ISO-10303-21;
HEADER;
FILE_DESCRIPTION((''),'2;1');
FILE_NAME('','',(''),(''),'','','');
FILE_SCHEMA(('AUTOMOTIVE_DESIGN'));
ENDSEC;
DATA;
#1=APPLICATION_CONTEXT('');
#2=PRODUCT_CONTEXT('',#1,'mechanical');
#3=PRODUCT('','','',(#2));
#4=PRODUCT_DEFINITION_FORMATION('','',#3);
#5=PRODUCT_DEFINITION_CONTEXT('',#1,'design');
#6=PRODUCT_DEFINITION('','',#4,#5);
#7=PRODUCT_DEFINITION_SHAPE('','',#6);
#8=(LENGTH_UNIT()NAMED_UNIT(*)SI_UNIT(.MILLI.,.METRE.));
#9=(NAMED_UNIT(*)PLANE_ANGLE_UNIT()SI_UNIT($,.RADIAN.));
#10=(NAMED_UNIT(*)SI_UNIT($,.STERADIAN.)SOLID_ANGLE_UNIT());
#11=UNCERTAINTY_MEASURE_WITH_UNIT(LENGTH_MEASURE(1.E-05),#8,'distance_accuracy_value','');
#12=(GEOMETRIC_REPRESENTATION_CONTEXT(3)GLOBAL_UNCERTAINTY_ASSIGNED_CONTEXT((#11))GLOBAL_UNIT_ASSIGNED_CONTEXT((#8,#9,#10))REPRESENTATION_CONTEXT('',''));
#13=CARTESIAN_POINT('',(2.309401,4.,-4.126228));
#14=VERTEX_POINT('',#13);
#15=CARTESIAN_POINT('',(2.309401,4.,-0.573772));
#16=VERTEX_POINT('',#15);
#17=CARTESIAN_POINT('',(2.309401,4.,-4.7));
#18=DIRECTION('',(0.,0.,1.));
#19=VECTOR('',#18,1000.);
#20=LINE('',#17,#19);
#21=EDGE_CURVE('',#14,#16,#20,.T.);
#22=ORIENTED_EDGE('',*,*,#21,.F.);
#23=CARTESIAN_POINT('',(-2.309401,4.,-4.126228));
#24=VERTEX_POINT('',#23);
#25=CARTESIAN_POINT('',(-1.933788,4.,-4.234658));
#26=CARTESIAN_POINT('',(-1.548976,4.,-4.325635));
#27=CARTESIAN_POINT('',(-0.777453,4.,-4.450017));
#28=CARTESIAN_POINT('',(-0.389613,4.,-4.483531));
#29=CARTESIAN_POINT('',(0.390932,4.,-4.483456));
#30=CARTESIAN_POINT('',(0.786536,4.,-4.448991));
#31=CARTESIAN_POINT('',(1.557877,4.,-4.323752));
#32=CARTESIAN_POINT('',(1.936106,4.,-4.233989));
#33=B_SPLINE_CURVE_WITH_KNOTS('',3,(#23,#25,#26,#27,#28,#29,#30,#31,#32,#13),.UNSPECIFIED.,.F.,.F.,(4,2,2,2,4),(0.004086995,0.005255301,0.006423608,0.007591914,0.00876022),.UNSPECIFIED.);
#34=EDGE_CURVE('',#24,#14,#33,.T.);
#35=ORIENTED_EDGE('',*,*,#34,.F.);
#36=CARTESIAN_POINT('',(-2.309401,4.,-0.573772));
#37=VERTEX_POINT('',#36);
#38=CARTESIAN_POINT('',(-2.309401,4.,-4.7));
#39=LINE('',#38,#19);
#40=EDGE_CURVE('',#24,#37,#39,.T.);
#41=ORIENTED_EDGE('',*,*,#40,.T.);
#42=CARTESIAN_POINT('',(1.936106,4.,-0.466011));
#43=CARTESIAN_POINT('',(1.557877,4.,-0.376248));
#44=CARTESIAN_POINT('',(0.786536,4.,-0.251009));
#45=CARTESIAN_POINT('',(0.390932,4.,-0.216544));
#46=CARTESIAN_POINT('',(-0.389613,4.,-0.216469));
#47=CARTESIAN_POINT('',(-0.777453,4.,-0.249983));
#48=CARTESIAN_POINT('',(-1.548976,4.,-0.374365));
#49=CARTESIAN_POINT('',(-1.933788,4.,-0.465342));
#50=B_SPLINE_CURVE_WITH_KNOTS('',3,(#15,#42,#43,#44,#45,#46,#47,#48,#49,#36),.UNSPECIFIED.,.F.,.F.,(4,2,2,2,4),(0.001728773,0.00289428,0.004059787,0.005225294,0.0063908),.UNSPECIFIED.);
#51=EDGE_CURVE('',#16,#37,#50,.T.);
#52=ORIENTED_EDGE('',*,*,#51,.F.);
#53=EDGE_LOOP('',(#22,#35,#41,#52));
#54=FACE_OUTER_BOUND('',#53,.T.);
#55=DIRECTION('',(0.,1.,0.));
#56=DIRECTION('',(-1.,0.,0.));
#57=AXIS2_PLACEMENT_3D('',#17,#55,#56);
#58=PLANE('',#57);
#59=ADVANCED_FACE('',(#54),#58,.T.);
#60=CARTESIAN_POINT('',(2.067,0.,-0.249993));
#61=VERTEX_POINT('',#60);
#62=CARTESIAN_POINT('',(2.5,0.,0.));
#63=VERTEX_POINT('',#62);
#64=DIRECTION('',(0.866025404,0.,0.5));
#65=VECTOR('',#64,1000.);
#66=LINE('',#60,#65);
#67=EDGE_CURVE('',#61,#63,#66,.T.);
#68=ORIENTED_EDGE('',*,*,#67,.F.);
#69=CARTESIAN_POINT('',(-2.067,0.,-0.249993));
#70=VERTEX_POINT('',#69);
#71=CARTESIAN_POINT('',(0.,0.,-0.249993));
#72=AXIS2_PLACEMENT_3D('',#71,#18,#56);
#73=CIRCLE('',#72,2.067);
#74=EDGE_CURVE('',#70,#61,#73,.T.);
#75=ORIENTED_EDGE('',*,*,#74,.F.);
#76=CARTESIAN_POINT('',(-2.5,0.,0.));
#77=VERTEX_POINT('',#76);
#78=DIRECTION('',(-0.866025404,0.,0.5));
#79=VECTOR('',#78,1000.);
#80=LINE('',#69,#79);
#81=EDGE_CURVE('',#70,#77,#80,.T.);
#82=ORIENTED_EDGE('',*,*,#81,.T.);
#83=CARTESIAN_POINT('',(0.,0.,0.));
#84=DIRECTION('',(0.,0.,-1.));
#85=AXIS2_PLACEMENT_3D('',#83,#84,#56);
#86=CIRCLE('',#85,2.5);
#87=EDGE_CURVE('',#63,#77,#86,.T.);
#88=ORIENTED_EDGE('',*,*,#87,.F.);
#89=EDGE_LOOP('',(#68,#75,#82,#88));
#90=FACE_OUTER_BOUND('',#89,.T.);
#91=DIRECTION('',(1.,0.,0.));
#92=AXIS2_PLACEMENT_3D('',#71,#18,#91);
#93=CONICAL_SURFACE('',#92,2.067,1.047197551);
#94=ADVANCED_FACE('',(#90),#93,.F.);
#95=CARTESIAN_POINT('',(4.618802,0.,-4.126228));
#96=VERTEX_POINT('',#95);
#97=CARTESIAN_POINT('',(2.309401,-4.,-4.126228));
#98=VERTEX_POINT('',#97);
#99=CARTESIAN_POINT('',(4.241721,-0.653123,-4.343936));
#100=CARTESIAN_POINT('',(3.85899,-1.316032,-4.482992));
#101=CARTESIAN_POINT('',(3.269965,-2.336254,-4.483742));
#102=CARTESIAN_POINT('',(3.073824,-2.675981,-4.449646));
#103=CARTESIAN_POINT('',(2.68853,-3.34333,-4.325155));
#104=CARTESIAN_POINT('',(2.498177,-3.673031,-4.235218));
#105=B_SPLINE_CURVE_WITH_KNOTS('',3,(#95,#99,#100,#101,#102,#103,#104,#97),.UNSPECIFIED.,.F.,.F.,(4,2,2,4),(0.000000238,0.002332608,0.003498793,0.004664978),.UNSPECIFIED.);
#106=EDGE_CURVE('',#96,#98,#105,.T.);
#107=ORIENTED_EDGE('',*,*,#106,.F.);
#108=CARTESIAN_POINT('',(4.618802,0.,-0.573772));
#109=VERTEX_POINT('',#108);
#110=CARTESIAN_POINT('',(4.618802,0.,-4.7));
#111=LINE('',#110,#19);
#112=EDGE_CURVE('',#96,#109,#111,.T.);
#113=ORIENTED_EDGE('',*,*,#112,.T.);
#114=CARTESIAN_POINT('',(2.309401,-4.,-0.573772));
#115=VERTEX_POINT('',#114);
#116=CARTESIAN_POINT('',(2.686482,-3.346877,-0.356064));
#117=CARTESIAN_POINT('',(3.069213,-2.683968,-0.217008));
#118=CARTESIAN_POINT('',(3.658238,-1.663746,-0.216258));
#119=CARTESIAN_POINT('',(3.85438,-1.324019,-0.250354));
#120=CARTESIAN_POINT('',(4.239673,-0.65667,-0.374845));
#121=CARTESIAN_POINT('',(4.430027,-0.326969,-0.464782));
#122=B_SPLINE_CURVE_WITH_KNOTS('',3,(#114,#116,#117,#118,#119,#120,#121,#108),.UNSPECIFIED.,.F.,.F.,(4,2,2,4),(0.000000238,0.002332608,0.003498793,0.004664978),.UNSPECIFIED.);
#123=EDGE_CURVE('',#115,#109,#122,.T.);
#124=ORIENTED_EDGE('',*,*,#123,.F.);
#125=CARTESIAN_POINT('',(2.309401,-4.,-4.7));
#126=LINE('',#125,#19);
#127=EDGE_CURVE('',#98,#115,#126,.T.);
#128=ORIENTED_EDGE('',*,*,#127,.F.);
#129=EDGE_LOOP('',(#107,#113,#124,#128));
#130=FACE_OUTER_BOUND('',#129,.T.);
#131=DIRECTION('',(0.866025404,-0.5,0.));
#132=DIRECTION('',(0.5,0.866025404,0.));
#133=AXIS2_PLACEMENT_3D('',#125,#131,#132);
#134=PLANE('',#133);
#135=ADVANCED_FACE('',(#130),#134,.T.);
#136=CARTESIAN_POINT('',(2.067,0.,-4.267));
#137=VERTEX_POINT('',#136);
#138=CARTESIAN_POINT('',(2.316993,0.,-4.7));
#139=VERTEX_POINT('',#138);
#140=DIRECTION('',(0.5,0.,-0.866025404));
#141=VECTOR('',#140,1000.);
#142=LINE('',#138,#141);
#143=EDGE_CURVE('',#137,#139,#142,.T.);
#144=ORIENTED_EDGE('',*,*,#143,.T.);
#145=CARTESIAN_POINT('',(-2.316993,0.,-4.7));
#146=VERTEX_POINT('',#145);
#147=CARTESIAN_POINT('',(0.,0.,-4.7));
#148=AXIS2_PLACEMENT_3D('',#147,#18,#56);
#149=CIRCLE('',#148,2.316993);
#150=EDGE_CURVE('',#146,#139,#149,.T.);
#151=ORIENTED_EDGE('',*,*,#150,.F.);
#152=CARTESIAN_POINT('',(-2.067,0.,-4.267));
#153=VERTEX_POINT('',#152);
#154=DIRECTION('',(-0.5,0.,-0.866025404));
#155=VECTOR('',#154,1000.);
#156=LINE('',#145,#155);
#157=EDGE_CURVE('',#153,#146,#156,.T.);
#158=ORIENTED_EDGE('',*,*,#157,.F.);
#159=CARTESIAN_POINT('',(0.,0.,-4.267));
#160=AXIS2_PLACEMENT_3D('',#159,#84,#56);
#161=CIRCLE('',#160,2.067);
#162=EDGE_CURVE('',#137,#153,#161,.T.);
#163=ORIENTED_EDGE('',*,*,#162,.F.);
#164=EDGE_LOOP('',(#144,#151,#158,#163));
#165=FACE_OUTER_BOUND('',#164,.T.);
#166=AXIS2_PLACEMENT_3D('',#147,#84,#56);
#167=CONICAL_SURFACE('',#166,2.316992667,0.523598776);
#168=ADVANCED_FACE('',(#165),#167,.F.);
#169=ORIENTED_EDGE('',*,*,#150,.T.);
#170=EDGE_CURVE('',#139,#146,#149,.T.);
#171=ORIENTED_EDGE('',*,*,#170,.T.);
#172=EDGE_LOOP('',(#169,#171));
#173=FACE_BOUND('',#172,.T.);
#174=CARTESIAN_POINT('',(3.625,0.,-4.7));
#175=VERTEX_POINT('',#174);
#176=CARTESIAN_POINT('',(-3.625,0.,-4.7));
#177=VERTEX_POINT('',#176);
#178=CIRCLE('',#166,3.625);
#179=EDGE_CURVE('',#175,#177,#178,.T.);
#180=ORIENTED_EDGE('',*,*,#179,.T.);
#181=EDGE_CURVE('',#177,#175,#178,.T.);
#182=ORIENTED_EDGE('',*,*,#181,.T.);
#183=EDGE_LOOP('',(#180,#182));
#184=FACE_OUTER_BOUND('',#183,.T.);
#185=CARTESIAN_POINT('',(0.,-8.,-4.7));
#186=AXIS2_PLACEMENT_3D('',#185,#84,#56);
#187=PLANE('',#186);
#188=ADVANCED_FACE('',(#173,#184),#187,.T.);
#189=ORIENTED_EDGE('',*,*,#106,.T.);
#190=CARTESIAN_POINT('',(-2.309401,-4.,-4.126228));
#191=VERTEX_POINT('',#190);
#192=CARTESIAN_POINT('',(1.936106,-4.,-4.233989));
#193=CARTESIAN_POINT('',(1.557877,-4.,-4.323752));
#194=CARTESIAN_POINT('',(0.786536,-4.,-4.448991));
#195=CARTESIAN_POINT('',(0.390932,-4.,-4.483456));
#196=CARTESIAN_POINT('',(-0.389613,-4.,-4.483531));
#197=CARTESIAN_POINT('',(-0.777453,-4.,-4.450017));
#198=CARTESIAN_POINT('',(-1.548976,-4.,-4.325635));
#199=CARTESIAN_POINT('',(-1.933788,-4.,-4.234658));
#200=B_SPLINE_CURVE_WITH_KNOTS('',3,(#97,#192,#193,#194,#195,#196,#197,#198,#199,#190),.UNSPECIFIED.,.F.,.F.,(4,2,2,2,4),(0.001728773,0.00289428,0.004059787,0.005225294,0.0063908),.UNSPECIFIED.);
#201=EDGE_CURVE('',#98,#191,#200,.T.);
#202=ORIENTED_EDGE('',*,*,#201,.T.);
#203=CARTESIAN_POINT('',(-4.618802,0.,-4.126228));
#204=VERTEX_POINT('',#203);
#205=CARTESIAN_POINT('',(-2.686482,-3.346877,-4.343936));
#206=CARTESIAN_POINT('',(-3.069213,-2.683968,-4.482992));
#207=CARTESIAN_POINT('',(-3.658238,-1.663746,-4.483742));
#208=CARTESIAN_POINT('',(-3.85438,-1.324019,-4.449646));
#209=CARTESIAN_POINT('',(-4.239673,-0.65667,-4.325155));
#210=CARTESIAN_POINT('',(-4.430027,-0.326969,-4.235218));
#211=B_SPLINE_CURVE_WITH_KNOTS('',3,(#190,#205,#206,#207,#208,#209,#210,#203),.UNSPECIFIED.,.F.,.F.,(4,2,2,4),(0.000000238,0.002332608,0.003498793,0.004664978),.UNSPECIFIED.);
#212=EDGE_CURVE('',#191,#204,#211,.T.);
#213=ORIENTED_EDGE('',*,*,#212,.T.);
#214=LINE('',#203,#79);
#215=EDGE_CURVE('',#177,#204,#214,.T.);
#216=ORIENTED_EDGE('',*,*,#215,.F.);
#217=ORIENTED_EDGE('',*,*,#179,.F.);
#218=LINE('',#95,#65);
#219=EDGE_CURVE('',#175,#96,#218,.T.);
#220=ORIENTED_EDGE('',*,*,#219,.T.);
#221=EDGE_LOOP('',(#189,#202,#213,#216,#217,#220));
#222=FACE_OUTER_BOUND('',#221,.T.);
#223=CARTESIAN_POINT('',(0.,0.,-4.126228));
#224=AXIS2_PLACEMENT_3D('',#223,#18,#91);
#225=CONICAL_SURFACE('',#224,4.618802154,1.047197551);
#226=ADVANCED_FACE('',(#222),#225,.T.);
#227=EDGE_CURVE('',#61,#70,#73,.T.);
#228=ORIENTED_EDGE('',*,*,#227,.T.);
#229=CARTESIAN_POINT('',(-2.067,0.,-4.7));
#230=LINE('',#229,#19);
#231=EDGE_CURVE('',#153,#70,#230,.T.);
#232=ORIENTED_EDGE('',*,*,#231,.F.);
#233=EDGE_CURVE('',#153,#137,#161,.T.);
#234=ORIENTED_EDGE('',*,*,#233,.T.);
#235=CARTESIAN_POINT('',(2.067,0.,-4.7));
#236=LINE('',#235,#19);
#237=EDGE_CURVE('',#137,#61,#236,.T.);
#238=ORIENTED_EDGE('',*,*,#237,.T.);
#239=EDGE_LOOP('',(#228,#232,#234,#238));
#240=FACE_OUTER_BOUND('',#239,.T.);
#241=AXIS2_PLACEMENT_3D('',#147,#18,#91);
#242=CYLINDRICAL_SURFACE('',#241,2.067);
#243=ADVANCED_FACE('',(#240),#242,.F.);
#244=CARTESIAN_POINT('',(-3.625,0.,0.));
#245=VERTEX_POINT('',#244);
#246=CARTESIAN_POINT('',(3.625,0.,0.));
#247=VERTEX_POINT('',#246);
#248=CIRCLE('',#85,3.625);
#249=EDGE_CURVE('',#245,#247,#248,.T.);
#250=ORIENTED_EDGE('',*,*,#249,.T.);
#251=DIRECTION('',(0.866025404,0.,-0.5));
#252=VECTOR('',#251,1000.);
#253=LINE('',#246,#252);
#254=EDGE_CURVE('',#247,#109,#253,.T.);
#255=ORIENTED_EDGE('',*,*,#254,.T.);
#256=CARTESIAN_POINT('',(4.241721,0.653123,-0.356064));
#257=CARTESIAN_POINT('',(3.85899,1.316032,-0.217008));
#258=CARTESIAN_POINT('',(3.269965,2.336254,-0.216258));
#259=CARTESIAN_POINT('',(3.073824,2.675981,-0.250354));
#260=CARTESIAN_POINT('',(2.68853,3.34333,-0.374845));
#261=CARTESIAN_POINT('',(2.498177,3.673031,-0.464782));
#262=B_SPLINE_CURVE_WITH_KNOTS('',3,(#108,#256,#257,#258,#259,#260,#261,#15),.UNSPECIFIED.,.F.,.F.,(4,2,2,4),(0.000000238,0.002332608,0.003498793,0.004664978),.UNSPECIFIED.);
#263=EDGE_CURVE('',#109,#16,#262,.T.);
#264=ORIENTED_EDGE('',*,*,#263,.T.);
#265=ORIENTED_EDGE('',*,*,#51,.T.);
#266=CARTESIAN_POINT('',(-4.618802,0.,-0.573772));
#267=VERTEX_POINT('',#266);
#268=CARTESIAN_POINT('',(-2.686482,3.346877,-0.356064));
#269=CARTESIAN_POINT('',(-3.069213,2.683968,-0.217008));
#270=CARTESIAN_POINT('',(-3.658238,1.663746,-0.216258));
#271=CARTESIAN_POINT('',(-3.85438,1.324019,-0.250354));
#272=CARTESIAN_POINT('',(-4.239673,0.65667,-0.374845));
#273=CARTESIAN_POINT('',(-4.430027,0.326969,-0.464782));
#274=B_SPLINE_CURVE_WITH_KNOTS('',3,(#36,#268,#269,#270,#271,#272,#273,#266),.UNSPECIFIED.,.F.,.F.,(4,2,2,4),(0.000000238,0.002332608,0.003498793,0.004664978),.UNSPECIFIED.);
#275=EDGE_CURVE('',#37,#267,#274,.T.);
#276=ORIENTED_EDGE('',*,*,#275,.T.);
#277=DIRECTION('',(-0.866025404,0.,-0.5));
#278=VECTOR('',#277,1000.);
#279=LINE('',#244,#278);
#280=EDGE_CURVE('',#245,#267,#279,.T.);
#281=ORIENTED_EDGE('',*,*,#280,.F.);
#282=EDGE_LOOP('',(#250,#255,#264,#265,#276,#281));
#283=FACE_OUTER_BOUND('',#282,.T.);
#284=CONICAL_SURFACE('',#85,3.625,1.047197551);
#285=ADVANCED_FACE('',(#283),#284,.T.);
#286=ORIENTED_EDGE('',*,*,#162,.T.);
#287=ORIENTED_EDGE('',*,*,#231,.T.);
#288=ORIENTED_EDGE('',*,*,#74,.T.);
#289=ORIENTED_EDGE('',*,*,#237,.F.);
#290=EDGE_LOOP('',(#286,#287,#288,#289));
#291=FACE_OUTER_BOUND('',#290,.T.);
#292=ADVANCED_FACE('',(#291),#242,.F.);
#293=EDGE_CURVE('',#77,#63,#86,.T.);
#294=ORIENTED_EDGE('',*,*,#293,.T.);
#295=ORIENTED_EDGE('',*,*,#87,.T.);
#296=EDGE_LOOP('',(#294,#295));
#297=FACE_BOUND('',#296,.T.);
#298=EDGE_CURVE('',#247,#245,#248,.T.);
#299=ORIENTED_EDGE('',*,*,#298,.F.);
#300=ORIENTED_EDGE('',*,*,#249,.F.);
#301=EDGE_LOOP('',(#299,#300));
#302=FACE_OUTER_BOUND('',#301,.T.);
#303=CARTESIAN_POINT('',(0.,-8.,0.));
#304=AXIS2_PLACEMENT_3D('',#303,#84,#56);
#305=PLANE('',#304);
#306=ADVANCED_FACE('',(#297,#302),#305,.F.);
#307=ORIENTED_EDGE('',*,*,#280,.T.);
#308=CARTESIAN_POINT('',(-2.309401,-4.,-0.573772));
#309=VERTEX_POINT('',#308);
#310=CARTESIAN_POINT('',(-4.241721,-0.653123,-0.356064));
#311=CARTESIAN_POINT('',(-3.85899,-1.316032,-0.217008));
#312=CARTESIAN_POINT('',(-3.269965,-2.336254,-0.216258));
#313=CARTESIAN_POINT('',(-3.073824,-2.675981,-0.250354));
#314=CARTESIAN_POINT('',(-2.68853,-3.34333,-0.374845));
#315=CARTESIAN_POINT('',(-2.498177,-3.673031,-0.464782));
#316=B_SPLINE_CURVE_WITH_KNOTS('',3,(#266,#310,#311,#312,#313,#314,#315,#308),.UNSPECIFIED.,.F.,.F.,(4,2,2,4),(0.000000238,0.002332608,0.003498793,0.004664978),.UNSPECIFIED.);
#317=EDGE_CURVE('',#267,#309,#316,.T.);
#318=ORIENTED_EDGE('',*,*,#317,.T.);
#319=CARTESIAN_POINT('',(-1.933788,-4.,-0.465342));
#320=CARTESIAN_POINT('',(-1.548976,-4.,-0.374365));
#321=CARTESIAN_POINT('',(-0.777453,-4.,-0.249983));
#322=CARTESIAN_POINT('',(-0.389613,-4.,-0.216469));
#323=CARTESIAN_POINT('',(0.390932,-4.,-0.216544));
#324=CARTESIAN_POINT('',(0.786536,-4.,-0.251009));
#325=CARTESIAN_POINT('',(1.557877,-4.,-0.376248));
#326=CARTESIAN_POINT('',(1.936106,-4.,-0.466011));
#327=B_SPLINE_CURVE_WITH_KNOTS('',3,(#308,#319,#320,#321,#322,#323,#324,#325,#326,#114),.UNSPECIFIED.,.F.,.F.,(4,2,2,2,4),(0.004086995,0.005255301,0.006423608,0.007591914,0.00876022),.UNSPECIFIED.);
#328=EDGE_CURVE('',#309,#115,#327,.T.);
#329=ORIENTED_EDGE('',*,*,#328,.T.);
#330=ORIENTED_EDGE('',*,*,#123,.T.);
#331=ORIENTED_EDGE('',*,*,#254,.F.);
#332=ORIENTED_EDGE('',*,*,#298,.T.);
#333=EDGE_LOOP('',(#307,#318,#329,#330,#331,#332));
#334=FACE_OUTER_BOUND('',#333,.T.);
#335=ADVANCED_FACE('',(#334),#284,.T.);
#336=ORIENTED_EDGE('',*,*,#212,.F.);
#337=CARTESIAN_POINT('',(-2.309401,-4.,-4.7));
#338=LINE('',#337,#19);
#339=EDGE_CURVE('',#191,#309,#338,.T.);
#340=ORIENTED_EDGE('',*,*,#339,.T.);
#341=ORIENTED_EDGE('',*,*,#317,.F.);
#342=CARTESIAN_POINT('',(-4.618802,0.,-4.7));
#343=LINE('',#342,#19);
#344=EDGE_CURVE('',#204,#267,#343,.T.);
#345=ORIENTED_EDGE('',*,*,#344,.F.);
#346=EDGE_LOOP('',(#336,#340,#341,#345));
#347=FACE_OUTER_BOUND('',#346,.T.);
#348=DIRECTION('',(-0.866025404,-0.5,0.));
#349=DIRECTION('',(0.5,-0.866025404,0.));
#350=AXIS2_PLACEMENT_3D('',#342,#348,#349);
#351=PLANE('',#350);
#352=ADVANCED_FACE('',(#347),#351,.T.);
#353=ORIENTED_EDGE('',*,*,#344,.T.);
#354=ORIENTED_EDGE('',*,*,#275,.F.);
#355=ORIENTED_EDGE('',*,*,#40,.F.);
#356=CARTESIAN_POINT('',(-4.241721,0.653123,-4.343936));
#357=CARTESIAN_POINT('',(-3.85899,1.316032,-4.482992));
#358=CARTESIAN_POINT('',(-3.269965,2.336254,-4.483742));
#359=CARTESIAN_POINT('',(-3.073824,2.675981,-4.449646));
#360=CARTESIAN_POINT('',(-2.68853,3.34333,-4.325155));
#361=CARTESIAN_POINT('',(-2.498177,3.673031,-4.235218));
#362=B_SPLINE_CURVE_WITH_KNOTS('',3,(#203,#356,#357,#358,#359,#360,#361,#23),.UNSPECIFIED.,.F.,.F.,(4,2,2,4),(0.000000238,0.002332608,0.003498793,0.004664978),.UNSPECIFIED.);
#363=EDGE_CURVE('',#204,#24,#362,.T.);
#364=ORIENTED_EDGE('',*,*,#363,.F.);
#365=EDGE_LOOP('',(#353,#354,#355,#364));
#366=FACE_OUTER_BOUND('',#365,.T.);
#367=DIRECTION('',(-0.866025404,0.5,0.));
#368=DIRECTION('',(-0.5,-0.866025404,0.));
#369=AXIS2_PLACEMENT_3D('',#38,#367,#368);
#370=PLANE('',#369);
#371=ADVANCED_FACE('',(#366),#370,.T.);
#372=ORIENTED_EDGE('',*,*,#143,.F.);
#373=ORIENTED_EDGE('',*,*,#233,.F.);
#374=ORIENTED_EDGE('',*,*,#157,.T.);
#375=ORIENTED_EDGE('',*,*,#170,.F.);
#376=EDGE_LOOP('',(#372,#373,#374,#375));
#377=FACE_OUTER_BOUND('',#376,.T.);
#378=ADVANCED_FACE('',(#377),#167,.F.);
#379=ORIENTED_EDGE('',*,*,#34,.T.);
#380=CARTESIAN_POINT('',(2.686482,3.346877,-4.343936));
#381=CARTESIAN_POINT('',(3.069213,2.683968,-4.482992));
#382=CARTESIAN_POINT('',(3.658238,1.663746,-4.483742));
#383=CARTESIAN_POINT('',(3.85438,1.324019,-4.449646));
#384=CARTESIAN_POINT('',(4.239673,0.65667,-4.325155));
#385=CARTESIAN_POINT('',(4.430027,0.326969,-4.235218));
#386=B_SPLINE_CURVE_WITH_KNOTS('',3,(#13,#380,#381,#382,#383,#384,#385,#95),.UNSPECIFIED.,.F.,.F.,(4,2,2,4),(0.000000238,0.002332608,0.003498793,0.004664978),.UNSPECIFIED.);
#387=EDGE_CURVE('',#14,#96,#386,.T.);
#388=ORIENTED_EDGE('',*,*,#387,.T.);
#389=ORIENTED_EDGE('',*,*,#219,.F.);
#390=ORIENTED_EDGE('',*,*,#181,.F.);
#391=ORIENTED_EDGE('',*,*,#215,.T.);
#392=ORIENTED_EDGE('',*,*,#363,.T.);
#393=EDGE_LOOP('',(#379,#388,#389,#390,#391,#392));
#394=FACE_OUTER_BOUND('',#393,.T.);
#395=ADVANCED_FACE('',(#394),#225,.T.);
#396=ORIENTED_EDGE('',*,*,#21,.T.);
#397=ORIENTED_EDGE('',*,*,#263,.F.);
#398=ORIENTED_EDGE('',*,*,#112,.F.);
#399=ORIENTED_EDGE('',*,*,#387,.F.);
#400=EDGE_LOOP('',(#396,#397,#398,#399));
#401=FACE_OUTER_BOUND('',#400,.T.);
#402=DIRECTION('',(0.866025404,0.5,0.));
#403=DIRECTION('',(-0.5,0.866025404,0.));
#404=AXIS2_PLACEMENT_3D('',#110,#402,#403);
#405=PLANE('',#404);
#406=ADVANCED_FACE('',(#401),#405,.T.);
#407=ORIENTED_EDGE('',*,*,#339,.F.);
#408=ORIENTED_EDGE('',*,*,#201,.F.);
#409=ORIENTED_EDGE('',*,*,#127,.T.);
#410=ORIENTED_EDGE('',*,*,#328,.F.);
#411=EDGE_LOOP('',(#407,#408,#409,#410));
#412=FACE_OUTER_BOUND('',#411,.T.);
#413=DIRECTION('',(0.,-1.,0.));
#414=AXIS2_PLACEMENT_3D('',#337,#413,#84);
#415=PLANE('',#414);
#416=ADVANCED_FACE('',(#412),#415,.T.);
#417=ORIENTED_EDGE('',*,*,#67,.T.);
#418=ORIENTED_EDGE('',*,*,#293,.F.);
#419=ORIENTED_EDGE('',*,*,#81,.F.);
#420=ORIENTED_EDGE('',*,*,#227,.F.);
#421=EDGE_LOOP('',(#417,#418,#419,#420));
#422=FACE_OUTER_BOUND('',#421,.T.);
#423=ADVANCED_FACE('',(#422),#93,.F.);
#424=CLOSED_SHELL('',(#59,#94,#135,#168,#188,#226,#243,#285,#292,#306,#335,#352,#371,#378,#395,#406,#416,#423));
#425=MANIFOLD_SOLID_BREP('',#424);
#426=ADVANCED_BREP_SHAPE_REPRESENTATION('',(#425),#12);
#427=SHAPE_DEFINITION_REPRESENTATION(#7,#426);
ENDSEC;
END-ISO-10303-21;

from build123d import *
from OCP.BRepFilletAPI import BRepFilletAPI_MakeChamfer

# Parameters (mm, degrees)
SKETCH1_R        = 2.067
BASENUT_DEPTH    = 4.7
ENDCHAMFER_SIZE  = 0.433
ENDCHAMFER_SIZE2 = 0.249992667


with BuildPart() as part:
    # Sketch1 → BaseNut (new body)
    with BuildSketch(Plane.XY):
        Polygon((4.618802154, 0), (2.309401077, 4), (-2.309401077, 4), (-4.618802154, 0), (-2.309401077, -4), (2.309401077, -4), align=None)
        Circle(SKETCH1_R, mode=Mode.SUBTRACT)
    extrude(amount=-BASENUT_DEPTH)

    # Sketch2 → Double-Chamfer (revolve, cut)
    with BuildSketch(Plane(origin=(0, 0, 0), x_dir=(1, 0, 0), z_dir=(0, 1, 0))):
        Polygon((-4.618802154, 4.7), (-3.625, 4.7), (-4.618802154, 4.126228059), align=None)
        Polygon((-4.618802154, 0.573771941), (-4.618802154, 0), (-3.625, 0), align=None)
    revolve(axis=Axis((0, 0, -3.375940562), (0, 0, 1)), mode=Mode.SUBTRACT)

    # EndChamfer: one chamfer whose edges measure the first distance from different faces: ONE call of the kernel's chamfer builder (chamfer() names one face for all edges)
    endchamfer_edges_1 = [part.edges().sort_by_distance(p)[0] for p in [
        (-2.067, 0, -4.7),
    ]]
    endchamfer_side_1 = [part.faces().sort_by_distance(p)[0] for p in [
        (-2.067, 0, -2.35),
    ]]
    endchamfer_edges_2 = [part.edges().sort_by_distance(p)[0] for p in [
        (-2.067, 0, 0),
    ]]
    endchamfer_side_2 = [part.faces().sort_by_distance(p)[0] for p in [
        (3.522469517, 0, 0),
    ]]
    endchamfer = BRepFilletAPI_MakeChamfer(part.part.solid().wrapped)
    for e in endchamfer_edges_1:
        endchamfer.Add(ENDCHAMFER_SIZE, ENDCHAMFER_SIZE2, e.wrapped, endchamfer_side_1[0].wrapped)  # the first distance lies on this face
    for e in endchamfer_edges_2:
        endchamfer.Add(ENDCHAMFER_SIZE, ENDCHAMFER_SIZE2, e.wrapped, endchamfer_side_2[0].wrapped)  # the first distance lies on this face
    add(Compound.cast(endchamfer.Shape()), mode=Mode.REPLACE)


solid = part.part
